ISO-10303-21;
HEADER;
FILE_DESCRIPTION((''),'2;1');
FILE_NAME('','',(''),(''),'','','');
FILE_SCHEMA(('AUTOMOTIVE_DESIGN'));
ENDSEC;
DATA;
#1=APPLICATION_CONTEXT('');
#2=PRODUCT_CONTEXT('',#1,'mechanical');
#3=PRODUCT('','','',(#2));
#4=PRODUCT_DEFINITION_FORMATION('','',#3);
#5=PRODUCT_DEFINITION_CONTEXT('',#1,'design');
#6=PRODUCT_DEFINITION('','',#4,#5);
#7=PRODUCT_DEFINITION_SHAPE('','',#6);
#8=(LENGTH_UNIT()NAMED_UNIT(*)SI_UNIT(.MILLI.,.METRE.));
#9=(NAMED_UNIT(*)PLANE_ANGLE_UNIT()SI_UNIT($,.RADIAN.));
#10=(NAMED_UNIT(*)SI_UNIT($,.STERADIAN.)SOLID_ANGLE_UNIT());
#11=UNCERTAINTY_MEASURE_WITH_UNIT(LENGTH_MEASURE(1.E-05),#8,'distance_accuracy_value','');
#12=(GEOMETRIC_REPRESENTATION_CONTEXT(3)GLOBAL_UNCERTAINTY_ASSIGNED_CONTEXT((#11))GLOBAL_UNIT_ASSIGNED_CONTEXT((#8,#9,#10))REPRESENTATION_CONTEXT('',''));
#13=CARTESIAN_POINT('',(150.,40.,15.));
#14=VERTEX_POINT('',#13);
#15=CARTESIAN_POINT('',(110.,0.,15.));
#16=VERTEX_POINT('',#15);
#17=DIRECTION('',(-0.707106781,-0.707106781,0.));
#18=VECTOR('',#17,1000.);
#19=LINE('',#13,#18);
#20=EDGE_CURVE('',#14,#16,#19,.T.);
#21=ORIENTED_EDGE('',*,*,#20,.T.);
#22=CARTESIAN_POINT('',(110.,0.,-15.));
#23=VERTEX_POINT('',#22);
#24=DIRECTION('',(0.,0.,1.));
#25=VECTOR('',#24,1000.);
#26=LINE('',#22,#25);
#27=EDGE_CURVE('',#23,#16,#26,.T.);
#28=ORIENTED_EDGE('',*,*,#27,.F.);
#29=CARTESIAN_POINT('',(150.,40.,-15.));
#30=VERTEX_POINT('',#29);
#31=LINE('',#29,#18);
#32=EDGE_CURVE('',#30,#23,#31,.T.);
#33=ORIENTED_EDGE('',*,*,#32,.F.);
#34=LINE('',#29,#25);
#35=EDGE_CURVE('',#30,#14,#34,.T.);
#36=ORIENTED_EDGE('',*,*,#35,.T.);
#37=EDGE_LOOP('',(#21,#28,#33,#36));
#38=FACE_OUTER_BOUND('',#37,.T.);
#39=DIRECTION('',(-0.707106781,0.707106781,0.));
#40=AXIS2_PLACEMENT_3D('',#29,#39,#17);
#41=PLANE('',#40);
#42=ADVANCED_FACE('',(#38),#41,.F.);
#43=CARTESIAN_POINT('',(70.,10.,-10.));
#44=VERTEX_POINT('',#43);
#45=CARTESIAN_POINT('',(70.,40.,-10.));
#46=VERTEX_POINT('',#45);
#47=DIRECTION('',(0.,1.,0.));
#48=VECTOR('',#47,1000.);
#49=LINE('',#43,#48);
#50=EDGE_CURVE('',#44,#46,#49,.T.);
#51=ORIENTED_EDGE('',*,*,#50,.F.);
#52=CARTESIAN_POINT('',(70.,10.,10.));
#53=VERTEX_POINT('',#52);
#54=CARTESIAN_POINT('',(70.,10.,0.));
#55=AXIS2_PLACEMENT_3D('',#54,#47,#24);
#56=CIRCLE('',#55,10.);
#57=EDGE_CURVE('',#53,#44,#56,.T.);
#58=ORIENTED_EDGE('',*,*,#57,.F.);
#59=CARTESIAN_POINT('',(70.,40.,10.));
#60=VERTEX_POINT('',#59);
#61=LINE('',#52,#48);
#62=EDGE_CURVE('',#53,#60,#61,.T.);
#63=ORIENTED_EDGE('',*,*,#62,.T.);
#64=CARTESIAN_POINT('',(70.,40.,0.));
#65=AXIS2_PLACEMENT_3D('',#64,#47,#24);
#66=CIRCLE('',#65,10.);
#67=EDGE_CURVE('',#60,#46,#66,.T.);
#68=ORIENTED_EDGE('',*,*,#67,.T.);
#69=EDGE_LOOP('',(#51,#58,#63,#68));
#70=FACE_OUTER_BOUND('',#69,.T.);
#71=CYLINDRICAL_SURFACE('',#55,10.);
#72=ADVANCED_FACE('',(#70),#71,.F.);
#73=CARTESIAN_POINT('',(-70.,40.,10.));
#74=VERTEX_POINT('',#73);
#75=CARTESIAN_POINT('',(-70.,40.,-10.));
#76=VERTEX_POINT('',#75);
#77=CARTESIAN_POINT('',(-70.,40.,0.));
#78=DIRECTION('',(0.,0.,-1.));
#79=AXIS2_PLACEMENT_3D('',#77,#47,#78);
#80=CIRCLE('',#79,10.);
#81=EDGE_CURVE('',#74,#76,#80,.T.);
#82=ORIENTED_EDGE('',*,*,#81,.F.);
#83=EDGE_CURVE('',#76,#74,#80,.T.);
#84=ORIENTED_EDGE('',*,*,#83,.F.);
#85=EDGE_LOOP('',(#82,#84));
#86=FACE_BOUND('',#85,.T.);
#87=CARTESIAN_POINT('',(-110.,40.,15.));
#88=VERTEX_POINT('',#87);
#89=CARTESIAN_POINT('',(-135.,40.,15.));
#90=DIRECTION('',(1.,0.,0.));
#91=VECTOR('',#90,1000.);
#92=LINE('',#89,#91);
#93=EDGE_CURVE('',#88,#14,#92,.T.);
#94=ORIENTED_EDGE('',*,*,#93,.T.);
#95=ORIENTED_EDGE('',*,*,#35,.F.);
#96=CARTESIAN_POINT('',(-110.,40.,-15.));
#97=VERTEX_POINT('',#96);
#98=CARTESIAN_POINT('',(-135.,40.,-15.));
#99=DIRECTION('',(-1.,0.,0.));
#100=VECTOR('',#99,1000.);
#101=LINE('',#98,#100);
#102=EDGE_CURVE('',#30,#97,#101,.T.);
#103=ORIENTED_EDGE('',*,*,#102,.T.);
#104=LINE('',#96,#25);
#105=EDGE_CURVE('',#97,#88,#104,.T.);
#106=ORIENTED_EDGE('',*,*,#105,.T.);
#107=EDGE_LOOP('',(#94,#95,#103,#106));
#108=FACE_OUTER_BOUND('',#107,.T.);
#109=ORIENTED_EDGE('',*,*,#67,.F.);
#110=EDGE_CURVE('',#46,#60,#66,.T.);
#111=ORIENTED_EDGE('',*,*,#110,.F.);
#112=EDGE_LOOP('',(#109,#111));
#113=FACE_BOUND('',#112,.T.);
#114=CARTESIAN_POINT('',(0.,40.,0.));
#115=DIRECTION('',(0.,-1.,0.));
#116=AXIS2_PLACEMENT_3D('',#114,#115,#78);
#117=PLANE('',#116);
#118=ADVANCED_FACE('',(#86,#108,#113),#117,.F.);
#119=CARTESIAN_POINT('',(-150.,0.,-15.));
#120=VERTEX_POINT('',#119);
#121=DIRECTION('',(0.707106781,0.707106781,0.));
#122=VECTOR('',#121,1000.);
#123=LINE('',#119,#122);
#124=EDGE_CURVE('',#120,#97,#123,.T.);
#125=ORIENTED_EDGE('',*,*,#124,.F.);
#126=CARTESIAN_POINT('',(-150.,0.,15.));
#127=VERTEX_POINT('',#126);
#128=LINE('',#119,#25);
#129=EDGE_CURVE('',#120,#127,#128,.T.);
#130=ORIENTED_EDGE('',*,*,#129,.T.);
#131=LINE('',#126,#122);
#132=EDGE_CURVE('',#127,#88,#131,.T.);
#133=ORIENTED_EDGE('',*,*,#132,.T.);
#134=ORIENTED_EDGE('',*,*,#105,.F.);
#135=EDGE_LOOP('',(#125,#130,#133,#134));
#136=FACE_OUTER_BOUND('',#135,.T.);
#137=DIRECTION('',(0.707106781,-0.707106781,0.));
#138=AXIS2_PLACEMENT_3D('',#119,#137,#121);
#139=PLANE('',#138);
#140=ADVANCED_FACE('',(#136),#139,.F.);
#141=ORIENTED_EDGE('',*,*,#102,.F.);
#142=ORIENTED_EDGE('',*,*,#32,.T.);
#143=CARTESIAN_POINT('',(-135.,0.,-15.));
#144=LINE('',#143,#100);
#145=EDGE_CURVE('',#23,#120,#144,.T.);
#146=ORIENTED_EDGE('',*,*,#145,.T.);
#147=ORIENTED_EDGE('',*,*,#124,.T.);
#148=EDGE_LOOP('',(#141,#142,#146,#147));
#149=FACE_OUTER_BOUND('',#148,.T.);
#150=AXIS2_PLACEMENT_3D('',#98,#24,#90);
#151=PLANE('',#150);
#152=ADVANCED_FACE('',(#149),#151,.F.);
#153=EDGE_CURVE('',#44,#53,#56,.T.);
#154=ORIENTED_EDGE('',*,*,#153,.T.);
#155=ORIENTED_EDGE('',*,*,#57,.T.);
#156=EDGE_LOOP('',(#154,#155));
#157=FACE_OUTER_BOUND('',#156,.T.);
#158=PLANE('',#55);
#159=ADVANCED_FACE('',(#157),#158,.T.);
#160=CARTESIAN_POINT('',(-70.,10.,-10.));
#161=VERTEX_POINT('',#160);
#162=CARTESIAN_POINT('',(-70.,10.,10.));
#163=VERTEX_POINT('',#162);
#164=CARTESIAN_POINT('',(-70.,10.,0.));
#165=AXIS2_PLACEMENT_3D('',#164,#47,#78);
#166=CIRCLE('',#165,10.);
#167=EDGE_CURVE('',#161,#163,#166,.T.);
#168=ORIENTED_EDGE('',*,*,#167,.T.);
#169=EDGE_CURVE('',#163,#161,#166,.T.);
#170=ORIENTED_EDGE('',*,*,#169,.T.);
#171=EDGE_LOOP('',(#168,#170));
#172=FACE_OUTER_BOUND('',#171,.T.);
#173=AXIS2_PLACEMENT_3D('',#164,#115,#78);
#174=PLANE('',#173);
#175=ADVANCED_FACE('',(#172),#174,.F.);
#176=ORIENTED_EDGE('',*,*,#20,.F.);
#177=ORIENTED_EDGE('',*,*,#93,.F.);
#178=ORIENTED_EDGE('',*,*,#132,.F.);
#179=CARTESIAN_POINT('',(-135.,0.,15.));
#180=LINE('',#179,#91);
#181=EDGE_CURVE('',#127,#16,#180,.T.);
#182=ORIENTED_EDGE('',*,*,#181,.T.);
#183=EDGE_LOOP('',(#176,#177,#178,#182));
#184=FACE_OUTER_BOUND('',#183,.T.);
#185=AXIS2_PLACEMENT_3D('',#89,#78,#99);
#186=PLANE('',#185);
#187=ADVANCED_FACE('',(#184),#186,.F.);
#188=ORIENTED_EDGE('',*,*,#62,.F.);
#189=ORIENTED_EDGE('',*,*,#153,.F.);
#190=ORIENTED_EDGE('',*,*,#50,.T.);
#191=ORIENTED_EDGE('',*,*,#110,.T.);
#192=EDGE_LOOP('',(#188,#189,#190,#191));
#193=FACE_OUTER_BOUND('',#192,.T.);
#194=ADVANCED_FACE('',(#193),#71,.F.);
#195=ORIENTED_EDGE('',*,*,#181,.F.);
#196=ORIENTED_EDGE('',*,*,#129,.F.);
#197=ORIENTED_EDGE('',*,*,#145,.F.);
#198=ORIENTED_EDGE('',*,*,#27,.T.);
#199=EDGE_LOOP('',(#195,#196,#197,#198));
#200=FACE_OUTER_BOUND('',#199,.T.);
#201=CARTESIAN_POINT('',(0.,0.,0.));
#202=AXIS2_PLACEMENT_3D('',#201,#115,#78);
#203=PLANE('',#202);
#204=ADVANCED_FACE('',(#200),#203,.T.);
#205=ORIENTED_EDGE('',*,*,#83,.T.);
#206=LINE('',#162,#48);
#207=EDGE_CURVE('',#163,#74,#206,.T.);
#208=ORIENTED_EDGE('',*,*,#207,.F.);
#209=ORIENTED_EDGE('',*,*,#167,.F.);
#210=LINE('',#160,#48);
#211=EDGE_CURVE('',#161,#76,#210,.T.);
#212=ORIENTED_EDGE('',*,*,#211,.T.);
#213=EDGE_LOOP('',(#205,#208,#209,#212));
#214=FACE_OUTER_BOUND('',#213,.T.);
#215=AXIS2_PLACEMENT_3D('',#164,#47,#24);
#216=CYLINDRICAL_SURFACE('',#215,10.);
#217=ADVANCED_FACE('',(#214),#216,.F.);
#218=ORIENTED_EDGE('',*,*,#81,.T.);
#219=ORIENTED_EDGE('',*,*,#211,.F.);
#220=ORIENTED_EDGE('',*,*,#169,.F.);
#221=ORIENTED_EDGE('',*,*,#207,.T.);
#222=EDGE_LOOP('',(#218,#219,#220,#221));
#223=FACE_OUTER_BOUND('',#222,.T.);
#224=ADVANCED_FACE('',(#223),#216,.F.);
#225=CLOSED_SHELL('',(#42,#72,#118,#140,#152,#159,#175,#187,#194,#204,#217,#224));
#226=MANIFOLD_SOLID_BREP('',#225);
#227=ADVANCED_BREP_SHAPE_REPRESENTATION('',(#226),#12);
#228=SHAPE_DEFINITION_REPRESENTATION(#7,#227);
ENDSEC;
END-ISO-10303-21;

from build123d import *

# Parameters (mm, degrees)
SKETCH_1_W          = 270
SKETCH_1_H          = 30
EXTRUDE_1_DEPTH     = 40
SKETCH_2_R          = 10
CUT_EXTRUDE_2_DEPTH = 30
SKETCH_3_W          = 30
SKETCH_3_H          = 40
EXTRUDE_2_DEPTH     = 15
CUT_EXTRUDE_3_DEPTH = 159.113883008
SKETCH_5_W          = 30
SKETCH_5_H          = 40
EXTRUDE_3_DEPTH     = 15
CUT_EXTRUDE_4_DEPTH = 159.113883008


with BuildPart() as part:
    # 草图1 → 凸台-拉伸1 (new body)
    with BuildSketch(Plane(origin=(0, 0, 0), x_dir=(1, 0, 0), z_dir=(0, 1, 0))):
        Rectangle(SKETCH_1_W, SKETCH_1_H)
    extrude(amount=EXTRUDE_1_DEPTH)

    # 草图2 → 切除-拉伸2 (cut)
    with BuildSketch(Plane(origin=(0, 40, 0), x_dir=(1, 0, 0), z_dir=(0, 1, 0))):
        with Locations(Location((70, 0, 0), (0, 0, 270))):
            Circle(SKETCH_2_R)
        with Locations(Location((-70, 0, 0), (0, 0, 90))):
            Circle(SKETCH_2_R)
    extrude(amount=-CUT_EXTRUDE_2_DEPTH, mode=Mode.SUBTRACT)

    # 草图3 → 凸台-拉伸2 (add)
    with BuildSketch(Plane(origin=(135, 0, 0), x_dir=(0, 0, -1), z_dir=(1, 0, 0))):
        with Locations((0, 20)):
            Rectangle(SKETCH_3_W, SKETCH_3_H)
    extrude(amount=EXTRUDE_2_DEPTH)

    # 草图4 → 切除-拉伸3 (cut, through all)
    with BuildSketch(Plane.XY.offset(15)):
        Polygon((150, 40), (110, 0), (150, 0), align=None)
    extrude(amount=-CUT_EXTRUDE_3_DEPTH, mode=Mode.SUBTRACT)

    # 草图5 → 凸台-拉伸3 (add)
    with BuildSketch(Plane.ZY.offset(135)):
        with Locations((0, 20)):
            Rectangle(SKETCH_5_W, SKETCH_5_H)
    extrude(amount=EXTRUDE_3_DEPTH)

    # 草图6 → 切除-拉伸4 (cut, through all)
    with BuildSketch(Plane.XY.offset(15)):
        Polygon((-150, 0), (-110, 40), (-150, 40), align=None)
    extrude(amount=-CUT_EXTRUDE_4_DEPTH, mode=Mode.SUBTRACT)


solid = part.part
